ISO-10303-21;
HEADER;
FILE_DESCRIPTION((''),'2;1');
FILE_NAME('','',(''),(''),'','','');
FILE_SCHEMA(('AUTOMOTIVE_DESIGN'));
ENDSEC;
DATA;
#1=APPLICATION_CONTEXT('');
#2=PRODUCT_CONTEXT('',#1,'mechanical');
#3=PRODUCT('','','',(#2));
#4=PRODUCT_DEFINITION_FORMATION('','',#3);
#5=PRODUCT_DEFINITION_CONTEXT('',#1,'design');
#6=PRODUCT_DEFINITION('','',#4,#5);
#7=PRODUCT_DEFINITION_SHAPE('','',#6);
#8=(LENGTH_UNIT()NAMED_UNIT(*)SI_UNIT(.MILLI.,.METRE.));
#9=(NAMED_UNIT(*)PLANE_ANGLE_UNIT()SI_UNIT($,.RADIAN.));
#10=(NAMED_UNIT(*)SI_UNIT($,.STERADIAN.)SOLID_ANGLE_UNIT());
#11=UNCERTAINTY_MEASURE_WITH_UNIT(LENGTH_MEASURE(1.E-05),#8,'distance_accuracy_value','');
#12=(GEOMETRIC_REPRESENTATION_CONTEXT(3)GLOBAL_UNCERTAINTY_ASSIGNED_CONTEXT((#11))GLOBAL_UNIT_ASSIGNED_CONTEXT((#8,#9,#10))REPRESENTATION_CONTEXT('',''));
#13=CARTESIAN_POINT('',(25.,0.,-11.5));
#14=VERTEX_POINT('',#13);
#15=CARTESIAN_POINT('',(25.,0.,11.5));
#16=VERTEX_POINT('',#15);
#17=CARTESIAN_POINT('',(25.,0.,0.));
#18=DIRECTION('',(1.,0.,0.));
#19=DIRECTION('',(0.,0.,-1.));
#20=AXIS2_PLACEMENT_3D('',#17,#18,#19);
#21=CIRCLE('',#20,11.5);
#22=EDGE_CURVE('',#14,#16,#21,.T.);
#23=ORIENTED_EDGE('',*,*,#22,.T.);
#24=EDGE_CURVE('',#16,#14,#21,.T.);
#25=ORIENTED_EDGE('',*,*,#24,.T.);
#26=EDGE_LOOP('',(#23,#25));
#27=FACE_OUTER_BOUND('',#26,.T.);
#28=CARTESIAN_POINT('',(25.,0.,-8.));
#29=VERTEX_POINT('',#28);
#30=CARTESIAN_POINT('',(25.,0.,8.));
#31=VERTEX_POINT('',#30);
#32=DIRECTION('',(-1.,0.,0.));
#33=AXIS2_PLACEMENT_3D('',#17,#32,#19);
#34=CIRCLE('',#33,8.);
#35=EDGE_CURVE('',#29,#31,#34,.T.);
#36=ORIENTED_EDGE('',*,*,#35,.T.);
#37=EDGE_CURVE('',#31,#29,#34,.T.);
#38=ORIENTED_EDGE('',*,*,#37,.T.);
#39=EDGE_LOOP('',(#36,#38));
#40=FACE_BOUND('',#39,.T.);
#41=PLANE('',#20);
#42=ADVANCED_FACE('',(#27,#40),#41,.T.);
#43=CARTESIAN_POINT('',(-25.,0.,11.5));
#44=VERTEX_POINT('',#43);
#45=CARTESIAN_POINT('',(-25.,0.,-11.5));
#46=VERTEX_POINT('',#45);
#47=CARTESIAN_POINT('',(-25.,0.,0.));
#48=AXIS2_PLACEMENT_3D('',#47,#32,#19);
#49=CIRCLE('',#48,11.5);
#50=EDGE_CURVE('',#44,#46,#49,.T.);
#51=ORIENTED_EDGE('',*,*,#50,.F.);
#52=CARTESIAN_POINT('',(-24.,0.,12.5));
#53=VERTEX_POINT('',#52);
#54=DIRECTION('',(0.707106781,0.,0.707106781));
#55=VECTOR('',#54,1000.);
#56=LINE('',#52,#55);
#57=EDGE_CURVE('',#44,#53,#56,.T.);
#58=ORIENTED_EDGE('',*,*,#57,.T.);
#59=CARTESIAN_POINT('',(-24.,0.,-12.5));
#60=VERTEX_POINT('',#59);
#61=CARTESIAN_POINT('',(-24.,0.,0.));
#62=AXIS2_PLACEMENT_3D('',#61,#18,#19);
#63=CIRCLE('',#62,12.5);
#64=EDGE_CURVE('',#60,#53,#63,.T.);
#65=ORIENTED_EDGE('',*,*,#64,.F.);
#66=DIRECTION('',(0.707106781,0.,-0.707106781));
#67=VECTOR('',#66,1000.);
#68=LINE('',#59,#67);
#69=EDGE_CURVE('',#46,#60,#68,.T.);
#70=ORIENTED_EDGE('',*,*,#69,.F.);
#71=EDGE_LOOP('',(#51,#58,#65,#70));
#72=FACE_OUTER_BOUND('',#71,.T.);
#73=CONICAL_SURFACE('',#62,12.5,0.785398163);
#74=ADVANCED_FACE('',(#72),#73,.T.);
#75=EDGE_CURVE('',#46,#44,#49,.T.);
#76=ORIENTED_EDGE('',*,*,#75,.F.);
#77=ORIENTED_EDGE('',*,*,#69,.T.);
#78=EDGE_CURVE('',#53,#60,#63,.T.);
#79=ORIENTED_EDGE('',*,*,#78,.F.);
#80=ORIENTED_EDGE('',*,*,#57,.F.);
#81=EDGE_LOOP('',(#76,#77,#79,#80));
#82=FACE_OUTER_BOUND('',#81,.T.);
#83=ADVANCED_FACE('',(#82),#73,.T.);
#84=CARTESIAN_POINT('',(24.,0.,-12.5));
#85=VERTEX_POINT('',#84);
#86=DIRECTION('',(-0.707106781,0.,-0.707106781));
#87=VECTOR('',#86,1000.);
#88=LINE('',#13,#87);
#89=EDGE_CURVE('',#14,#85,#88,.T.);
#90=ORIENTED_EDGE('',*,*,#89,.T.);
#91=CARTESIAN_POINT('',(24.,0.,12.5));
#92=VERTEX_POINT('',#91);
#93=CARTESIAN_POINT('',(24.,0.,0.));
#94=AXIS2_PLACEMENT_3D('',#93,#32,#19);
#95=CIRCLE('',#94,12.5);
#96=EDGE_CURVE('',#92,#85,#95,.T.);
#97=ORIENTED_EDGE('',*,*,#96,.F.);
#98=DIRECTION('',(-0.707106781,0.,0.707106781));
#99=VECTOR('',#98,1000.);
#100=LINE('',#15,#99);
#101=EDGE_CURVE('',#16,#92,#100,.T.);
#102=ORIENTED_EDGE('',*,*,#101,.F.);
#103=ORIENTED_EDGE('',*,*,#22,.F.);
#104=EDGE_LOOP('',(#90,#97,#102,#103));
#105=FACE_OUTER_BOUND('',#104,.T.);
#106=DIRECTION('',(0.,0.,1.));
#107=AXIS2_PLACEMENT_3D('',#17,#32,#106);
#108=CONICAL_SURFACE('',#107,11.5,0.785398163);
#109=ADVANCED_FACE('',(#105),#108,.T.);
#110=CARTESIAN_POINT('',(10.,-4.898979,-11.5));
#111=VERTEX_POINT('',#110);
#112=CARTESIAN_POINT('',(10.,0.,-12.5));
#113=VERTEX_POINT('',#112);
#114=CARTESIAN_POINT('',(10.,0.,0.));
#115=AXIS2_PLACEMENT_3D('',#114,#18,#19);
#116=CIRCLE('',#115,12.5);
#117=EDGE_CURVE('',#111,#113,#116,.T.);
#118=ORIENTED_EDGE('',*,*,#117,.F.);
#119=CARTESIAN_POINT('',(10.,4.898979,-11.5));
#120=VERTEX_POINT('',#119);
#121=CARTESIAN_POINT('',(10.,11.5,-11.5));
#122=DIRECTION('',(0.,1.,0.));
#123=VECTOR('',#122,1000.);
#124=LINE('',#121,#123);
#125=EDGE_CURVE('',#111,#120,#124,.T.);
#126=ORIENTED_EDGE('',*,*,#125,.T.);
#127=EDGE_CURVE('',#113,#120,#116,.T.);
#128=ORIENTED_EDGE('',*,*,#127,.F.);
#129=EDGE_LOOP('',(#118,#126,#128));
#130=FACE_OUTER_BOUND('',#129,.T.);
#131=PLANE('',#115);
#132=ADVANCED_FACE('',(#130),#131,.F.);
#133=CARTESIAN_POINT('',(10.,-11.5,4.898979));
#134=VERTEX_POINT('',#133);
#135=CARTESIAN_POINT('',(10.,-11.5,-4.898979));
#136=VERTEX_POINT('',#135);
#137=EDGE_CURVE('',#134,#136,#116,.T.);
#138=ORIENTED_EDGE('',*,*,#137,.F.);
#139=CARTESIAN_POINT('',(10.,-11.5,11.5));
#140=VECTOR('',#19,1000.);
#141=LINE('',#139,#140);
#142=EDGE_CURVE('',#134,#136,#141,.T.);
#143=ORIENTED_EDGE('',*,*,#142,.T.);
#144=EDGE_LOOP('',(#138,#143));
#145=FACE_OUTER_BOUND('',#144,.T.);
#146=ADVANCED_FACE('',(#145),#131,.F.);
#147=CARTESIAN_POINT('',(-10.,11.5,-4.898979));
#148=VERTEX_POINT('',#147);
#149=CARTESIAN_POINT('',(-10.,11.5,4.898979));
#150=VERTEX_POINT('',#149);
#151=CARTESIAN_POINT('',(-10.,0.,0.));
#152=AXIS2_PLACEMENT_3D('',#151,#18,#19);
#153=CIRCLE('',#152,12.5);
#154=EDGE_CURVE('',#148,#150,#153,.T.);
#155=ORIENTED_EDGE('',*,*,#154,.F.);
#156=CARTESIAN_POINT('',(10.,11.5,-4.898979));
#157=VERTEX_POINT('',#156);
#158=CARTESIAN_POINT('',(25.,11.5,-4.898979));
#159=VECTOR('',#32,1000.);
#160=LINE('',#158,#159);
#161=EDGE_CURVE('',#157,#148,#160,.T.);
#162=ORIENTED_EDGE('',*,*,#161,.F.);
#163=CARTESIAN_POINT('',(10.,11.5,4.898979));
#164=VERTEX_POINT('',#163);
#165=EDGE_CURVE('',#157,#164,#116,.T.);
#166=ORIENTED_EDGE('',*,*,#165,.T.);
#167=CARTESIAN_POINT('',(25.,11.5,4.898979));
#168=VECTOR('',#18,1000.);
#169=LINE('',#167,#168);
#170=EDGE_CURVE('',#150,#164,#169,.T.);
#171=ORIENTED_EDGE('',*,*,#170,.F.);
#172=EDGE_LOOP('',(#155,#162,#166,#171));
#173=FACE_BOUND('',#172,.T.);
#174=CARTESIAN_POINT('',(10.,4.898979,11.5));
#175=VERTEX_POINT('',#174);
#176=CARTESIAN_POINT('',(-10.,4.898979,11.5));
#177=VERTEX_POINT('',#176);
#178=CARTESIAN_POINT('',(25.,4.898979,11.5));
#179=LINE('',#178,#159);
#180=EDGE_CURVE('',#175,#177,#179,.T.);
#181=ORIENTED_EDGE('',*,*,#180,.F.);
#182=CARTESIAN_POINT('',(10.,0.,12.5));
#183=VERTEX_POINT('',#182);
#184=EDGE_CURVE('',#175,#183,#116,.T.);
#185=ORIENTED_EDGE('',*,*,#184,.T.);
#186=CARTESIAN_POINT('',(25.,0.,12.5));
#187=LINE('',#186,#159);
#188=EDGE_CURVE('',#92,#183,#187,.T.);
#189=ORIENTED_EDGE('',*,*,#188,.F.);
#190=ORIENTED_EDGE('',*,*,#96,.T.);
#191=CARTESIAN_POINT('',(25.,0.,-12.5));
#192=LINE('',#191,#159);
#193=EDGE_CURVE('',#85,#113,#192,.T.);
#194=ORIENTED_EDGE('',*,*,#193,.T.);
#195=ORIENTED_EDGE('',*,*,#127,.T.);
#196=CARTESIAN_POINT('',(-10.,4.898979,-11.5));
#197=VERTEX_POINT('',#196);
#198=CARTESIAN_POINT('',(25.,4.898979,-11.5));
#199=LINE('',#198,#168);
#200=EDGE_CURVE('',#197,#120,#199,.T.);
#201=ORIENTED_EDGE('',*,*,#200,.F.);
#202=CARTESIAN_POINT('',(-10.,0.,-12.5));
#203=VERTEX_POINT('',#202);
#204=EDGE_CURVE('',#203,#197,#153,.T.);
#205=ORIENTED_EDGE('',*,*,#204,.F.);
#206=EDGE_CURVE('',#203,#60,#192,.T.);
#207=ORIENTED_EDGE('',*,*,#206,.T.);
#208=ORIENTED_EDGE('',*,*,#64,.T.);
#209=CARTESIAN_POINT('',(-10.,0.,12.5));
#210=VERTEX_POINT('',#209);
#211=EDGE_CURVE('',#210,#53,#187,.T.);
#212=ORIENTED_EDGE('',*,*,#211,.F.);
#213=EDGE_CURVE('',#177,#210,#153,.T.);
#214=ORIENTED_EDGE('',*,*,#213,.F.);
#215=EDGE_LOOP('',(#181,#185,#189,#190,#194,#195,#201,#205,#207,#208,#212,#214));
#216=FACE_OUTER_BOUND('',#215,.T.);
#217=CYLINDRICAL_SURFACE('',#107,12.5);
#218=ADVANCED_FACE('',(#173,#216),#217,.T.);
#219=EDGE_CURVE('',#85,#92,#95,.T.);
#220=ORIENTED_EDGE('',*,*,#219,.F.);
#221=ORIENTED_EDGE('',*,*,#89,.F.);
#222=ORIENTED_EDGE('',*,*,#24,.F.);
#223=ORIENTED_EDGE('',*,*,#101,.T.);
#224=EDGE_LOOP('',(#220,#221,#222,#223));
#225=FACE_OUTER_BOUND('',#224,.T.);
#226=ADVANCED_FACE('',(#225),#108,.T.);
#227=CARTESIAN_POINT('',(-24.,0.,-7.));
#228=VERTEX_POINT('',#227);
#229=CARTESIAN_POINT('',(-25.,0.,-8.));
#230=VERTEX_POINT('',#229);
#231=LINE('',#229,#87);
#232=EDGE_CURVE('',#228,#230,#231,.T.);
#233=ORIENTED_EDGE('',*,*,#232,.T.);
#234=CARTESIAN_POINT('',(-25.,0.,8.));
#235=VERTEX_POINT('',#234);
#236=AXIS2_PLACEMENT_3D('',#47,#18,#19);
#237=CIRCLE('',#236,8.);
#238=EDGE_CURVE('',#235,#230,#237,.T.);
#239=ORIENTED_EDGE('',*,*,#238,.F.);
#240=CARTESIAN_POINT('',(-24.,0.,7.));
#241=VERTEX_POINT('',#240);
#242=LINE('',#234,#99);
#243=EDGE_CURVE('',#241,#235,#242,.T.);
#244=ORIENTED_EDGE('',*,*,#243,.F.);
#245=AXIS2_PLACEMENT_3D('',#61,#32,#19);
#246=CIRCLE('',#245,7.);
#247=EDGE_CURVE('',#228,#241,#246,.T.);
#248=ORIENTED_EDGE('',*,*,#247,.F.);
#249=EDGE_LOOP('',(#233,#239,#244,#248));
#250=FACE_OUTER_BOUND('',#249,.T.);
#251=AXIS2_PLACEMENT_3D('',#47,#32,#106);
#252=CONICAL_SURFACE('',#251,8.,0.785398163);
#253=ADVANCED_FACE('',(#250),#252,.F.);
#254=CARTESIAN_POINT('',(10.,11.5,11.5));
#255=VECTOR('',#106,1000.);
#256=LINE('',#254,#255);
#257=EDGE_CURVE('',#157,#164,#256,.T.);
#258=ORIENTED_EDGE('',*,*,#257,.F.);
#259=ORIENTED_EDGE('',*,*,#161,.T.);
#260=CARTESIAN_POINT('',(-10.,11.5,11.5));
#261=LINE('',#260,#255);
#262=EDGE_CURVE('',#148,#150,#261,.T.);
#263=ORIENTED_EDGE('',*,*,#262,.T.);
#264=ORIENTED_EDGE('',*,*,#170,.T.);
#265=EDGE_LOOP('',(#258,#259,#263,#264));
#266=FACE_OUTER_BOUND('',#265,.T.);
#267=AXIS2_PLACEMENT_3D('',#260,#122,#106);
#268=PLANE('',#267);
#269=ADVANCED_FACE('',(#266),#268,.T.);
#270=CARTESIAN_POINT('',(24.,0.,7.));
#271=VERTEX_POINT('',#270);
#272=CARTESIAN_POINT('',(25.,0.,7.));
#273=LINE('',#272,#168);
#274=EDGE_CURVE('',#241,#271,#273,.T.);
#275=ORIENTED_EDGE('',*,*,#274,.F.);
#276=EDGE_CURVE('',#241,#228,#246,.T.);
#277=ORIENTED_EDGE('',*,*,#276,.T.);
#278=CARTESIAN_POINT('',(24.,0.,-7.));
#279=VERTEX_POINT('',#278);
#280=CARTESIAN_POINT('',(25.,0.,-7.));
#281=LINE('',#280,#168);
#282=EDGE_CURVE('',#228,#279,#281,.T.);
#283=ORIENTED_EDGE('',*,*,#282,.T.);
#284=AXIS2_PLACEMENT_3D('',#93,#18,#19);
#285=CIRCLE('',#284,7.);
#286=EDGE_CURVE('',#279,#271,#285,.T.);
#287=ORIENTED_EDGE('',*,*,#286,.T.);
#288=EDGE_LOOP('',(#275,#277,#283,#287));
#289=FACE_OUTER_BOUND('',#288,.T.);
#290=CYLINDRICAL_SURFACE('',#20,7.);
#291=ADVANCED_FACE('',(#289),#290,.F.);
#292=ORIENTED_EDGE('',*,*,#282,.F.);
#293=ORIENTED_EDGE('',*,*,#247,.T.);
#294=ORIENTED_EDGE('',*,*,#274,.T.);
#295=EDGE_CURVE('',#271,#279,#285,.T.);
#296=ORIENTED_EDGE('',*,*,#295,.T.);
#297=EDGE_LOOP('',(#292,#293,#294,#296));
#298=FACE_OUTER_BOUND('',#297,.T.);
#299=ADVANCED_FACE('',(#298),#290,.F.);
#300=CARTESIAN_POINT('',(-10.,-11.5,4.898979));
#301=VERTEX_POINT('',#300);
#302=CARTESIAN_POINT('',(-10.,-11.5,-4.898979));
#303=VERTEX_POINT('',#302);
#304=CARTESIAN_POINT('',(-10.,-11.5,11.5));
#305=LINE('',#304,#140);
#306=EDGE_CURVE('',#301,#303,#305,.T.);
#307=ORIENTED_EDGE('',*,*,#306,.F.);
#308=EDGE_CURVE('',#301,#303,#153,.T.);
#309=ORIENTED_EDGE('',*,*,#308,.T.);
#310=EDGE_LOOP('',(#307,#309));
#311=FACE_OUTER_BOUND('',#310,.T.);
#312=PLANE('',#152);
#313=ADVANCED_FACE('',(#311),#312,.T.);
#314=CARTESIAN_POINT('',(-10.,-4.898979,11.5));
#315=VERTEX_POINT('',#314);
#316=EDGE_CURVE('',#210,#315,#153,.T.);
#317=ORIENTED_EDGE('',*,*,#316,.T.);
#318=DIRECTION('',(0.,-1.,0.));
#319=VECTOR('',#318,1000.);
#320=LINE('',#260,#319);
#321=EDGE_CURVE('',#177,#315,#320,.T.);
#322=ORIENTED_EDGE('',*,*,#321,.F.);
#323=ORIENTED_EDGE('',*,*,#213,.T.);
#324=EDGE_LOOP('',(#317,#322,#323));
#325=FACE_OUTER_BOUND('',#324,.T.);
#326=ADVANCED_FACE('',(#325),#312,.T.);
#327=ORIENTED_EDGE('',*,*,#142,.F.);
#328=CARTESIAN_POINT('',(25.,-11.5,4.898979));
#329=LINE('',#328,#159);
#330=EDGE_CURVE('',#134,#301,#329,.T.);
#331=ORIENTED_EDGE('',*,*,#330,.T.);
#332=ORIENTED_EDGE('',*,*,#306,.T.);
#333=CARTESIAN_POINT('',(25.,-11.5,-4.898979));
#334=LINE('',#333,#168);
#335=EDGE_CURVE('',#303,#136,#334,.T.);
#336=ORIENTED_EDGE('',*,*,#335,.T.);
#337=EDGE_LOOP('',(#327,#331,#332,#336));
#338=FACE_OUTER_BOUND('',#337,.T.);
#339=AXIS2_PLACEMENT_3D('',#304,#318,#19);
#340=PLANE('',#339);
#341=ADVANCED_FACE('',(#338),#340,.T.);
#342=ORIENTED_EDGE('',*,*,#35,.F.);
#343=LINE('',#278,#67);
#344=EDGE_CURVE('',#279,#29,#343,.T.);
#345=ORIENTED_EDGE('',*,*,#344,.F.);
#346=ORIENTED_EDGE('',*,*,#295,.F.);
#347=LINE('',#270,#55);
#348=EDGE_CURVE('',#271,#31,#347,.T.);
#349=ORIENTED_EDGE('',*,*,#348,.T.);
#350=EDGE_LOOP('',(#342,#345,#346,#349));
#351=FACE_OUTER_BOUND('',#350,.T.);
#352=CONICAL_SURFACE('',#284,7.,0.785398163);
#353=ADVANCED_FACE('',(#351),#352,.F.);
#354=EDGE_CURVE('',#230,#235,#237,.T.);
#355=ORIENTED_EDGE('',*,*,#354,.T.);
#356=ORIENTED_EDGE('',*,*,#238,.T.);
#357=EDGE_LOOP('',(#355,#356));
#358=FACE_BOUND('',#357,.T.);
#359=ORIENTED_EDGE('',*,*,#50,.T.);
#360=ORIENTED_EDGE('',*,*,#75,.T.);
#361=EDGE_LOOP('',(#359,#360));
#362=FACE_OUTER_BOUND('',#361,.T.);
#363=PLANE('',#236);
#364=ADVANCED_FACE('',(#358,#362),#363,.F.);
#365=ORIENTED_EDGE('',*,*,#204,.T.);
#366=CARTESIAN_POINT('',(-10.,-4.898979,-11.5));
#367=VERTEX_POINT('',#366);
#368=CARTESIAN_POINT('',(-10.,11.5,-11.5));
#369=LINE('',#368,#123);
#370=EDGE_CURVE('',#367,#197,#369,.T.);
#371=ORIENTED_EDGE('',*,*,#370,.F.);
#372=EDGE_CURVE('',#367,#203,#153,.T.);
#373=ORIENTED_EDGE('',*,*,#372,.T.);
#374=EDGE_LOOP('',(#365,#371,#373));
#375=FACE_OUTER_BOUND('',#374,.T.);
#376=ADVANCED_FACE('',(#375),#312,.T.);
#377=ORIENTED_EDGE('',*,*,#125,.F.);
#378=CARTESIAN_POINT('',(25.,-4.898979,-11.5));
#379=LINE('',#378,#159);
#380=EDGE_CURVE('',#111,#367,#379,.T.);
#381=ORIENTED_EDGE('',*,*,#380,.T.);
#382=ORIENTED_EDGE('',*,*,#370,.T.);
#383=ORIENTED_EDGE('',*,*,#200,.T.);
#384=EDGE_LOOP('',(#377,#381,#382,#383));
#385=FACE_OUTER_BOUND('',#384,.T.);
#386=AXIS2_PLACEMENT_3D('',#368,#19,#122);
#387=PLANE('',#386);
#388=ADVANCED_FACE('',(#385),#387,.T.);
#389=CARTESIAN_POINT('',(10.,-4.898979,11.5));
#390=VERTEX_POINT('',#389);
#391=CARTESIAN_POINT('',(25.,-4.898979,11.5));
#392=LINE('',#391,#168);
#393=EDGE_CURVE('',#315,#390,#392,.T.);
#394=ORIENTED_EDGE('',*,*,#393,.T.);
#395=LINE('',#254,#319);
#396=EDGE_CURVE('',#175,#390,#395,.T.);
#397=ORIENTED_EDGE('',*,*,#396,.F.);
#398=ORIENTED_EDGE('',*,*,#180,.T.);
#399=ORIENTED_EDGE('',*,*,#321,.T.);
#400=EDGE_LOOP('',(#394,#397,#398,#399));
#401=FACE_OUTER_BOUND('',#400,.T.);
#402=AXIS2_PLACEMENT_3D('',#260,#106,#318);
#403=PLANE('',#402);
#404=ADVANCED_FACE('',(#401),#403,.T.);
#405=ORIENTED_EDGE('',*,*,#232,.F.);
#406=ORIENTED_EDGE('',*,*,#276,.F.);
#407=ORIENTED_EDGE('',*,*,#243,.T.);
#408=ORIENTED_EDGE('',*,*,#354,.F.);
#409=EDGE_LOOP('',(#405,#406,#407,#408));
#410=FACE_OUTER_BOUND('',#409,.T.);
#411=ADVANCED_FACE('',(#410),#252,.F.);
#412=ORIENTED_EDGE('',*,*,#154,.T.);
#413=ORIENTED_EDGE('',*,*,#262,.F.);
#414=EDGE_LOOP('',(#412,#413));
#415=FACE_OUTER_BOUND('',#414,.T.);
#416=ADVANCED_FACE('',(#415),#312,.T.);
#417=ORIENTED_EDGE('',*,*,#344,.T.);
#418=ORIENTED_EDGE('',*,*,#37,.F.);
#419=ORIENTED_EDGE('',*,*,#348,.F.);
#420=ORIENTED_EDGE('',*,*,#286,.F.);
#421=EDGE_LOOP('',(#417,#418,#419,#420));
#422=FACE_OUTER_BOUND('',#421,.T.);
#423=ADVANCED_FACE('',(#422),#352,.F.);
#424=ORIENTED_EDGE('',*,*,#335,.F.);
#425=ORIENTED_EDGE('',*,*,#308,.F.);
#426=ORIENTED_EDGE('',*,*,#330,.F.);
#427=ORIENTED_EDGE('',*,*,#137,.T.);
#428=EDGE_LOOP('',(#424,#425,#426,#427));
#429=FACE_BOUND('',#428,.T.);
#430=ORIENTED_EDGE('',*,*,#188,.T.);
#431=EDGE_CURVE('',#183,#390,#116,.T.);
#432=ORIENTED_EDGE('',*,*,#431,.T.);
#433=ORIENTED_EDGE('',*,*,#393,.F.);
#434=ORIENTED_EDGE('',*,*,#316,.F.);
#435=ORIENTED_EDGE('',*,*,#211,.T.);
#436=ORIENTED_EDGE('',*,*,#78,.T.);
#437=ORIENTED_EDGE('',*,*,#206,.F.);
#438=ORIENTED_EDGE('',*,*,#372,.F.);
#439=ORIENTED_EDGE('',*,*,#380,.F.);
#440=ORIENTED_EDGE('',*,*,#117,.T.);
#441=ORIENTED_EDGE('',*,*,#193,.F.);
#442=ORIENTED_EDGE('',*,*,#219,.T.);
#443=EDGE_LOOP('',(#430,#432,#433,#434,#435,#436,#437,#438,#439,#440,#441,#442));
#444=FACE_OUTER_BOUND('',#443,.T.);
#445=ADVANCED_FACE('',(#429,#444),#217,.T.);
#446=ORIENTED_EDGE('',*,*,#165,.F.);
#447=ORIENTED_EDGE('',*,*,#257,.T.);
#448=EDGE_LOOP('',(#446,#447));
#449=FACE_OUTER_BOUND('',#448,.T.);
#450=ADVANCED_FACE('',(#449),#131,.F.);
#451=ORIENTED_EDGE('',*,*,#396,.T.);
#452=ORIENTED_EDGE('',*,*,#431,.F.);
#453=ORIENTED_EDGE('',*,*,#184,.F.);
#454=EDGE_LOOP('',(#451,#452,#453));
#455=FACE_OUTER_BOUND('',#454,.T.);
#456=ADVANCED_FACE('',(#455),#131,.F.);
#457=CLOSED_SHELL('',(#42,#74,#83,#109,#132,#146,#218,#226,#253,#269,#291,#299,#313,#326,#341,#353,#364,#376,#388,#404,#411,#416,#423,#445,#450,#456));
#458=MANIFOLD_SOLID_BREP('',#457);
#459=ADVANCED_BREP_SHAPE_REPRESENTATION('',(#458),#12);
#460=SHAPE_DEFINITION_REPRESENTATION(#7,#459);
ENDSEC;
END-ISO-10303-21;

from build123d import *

# Parameters (mm, degrees)
SKETCH_1_R           = 12.5
EXTRUDE_1_DEPTH      = 25
HOLE_WIZARD_M16_1_D  = 14
SKETCH_4_OUTSIDE_W   = 39.248
SKETCH_4_OUTSIDE_H   = 39.248
SKETCH_4_OUTSIDE_W_2 = 23
SKETCH_4_OUTSIDE_H_2 = 23
CUT_EXTRUDE_1_DEPTH  = 10
CHAMFER_1_SIZE       = 1


with BuildPart() as part:
    # 草图1 → 凸台-拉伸1 (new, symmetric)
    with BuildSketch(Plane(origin=(0, 0, 0), x_dir=(0, 0, -1), z_dir=(1, 0, 0))):
        Circle(SKETCH_1_R)
    extrude(amount=EXTRUDE_1_DEPTH, both=True)

    # M16 螺纹孔1 (through all)
    with Locations(Plane(origin=(25, 0, 0), x_dir=(0, 0, -1), z_dir=(1, 0, 0))):
        with Locations((0, 0)):
            Hole(HOLE_WIZARD_M16_1_D / 2)

    # 草图4 outside → 切除-拉伸1 (cut, symmetric)
    with BuildSketch(Plane(origin=(0, 0, 0), x_dir=(0, 0, -1), z_dir=(1, 0, 0))):
        Rectangle(SKETCH_4_OUTSIDE_W, SKETCH_4_OUTSIDE_H)
        Rectangle(SKETCH_4_OUTSIDE_W_2, SKETCH_4_OUTSIDE_H_2, mode=Mode.SUBTRACT)
    extrude(amount=CUT_EXTRUDE_1_DEPTH, both=True, mode=Mode.SUBTRACT)

    # 倒角1
    chamfer_1_edges = [part.edges().sort_by_distance(p)[0] for p in [
        (-25, 0, 12.5),
        (25, 0, 12.5),
        (25, 0, -7),
        (-25, 0, -7),
    ]]
    chamfer(chamfer_1_edges, length=CHAMFER_1_SIZE)


solid = part.part
